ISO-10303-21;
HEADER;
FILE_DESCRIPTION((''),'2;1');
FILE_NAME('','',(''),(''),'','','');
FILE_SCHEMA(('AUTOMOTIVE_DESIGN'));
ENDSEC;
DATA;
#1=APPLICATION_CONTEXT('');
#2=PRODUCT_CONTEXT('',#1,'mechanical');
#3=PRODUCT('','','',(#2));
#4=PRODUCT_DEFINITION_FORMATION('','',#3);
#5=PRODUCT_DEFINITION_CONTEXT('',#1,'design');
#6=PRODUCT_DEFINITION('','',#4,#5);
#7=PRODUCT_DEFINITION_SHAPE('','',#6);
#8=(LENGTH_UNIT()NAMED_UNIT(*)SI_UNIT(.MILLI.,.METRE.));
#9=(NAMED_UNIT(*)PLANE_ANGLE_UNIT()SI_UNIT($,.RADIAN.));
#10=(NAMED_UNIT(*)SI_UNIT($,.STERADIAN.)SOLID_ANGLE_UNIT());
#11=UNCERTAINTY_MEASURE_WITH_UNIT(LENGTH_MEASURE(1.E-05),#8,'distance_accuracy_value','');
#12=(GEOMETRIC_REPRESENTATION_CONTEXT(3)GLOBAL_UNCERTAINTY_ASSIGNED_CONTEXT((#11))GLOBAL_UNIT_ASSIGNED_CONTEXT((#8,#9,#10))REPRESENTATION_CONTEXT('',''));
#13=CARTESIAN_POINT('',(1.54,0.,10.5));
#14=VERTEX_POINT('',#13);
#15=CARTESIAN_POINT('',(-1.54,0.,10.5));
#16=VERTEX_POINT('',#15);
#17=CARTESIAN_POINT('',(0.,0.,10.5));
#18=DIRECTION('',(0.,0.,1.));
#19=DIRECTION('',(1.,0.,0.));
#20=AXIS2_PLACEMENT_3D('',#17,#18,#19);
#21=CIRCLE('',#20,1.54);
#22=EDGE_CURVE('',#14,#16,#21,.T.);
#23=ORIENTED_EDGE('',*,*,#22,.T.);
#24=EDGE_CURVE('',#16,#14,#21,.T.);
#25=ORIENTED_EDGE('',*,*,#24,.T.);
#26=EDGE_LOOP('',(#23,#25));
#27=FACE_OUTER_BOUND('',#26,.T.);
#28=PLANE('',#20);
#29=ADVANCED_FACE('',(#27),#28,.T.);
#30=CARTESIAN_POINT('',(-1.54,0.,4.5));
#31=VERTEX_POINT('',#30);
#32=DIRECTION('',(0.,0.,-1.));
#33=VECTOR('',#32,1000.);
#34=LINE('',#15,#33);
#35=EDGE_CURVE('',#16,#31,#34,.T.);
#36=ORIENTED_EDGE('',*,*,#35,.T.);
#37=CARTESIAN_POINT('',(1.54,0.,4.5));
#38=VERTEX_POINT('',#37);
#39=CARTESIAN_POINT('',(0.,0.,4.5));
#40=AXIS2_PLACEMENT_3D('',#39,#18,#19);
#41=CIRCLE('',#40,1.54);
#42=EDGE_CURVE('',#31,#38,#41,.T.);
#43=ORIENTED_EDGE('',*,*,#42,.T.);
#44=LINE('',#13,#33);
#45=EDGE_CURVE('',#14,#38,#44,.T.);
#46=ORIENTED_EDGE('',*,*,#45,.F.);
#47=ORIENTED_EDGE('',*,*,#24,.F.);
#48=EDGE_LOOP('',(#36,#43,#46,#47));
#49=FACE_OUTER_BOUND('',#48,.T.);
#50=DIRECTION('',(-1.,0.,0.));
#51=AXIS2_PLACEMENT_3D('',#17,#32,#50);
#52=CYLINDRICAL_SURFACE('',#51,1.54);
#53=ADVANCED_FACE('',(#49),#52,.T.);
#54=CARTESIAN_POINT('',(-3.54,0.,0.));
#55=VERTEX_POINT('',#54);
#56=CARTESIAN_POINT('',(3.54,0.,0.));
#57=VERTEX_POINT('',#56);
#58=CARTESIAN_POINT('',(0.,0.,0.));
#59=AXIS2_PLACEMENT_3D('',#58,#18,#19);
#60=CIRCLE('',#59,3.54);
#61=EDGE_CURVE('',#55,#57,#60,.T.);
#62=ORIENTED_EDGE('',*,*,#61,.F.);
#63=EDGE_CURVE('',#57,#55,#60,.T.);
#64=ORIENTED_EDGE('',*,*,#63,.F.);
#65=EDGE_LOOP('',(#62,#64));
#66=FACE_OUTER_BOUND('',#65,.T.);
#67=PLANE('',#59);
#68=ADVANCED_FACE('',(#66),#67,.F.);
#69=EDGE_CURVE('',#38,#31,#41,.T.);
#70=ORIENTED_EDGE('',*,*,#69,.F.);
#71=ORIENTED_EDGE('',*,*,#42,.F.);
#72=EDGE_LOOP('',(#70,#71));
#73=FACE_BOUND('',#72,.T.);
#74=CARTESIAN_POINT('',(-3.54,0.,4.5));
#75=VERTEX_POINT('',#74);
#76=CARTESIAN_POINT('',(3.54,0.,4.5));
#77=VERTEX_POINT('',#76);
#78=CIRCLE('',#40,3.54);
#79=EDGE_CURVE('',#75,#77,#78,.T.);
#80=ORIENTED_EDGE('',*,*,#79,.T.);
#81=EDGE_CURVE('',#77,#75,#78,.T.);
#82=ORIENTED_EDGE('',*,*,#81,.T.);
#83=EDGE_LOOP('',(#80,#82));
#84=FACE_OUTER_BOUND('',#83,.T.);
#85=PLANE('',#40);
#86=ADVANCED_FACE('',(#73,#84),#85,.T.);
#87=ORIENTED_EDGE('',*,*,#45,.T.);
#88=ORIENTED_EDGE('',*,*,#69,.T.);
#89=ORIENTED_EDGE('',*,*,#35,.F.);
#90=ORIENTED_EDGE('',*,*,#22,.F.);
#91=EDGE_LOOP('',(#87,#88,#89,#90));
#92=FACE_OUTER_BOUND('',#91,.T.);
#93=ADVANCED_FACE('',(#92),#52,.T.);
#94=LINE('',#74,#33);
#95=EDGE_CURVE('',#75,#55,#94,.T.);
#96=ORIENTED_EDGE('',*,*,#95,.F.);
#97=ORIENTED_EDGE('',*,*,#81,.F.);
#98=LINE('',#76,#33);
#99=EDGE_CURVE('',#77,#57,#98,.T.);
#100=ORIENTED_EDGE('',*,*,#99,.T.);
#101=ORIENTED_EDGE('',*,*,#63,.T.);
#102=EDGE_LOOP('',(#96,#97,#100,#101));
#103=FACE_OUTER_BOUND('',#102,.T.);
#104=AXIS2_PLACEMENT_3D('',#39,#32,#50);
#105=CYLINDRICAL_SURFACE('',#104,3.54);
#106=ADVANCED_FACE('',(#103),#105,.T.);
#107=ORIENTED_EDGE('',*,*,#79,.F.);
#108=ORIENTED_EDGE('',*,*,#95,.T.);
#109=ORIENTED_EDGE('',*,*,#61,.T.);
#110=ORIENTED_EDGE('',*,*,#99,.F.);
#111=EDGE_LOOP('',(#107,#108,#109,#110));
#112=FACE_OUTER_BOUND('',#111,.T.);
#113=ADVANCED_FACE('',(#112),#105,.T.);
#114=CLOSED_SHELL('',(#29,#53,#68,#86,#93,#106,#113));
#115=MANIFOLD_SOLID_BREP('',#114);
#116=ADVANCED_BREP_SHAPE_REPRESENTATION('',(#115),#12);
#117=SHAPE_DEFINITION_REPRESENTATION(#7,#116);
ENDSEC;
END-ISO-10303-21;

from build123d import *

# Parameters (mm, degrees)
SKETCH_1_R      = 3.54
EXTRUDE_1_DEPTH = 4.5
SKETCH_2_R      = 1.54
EXTRUDE_2_DEPTH = 6


with BuildPart() as part:
    # 草图1 → 凸台-拉伸1 (new body)
    with BuildSketch(Plane.XY):
        Circle(SKETCH_1_R)
    extrude(amount=EXTRUDE_1_DEPTH)

    # 草图2 → 凸台-拉伸2 (add)
    with BuildSketch(Plane.XY.offset(4.5)):
        Circle(SKETCH_2_R)
    extrude(amount=EXTRUDE_2_DEPTH)


solid = part.part
